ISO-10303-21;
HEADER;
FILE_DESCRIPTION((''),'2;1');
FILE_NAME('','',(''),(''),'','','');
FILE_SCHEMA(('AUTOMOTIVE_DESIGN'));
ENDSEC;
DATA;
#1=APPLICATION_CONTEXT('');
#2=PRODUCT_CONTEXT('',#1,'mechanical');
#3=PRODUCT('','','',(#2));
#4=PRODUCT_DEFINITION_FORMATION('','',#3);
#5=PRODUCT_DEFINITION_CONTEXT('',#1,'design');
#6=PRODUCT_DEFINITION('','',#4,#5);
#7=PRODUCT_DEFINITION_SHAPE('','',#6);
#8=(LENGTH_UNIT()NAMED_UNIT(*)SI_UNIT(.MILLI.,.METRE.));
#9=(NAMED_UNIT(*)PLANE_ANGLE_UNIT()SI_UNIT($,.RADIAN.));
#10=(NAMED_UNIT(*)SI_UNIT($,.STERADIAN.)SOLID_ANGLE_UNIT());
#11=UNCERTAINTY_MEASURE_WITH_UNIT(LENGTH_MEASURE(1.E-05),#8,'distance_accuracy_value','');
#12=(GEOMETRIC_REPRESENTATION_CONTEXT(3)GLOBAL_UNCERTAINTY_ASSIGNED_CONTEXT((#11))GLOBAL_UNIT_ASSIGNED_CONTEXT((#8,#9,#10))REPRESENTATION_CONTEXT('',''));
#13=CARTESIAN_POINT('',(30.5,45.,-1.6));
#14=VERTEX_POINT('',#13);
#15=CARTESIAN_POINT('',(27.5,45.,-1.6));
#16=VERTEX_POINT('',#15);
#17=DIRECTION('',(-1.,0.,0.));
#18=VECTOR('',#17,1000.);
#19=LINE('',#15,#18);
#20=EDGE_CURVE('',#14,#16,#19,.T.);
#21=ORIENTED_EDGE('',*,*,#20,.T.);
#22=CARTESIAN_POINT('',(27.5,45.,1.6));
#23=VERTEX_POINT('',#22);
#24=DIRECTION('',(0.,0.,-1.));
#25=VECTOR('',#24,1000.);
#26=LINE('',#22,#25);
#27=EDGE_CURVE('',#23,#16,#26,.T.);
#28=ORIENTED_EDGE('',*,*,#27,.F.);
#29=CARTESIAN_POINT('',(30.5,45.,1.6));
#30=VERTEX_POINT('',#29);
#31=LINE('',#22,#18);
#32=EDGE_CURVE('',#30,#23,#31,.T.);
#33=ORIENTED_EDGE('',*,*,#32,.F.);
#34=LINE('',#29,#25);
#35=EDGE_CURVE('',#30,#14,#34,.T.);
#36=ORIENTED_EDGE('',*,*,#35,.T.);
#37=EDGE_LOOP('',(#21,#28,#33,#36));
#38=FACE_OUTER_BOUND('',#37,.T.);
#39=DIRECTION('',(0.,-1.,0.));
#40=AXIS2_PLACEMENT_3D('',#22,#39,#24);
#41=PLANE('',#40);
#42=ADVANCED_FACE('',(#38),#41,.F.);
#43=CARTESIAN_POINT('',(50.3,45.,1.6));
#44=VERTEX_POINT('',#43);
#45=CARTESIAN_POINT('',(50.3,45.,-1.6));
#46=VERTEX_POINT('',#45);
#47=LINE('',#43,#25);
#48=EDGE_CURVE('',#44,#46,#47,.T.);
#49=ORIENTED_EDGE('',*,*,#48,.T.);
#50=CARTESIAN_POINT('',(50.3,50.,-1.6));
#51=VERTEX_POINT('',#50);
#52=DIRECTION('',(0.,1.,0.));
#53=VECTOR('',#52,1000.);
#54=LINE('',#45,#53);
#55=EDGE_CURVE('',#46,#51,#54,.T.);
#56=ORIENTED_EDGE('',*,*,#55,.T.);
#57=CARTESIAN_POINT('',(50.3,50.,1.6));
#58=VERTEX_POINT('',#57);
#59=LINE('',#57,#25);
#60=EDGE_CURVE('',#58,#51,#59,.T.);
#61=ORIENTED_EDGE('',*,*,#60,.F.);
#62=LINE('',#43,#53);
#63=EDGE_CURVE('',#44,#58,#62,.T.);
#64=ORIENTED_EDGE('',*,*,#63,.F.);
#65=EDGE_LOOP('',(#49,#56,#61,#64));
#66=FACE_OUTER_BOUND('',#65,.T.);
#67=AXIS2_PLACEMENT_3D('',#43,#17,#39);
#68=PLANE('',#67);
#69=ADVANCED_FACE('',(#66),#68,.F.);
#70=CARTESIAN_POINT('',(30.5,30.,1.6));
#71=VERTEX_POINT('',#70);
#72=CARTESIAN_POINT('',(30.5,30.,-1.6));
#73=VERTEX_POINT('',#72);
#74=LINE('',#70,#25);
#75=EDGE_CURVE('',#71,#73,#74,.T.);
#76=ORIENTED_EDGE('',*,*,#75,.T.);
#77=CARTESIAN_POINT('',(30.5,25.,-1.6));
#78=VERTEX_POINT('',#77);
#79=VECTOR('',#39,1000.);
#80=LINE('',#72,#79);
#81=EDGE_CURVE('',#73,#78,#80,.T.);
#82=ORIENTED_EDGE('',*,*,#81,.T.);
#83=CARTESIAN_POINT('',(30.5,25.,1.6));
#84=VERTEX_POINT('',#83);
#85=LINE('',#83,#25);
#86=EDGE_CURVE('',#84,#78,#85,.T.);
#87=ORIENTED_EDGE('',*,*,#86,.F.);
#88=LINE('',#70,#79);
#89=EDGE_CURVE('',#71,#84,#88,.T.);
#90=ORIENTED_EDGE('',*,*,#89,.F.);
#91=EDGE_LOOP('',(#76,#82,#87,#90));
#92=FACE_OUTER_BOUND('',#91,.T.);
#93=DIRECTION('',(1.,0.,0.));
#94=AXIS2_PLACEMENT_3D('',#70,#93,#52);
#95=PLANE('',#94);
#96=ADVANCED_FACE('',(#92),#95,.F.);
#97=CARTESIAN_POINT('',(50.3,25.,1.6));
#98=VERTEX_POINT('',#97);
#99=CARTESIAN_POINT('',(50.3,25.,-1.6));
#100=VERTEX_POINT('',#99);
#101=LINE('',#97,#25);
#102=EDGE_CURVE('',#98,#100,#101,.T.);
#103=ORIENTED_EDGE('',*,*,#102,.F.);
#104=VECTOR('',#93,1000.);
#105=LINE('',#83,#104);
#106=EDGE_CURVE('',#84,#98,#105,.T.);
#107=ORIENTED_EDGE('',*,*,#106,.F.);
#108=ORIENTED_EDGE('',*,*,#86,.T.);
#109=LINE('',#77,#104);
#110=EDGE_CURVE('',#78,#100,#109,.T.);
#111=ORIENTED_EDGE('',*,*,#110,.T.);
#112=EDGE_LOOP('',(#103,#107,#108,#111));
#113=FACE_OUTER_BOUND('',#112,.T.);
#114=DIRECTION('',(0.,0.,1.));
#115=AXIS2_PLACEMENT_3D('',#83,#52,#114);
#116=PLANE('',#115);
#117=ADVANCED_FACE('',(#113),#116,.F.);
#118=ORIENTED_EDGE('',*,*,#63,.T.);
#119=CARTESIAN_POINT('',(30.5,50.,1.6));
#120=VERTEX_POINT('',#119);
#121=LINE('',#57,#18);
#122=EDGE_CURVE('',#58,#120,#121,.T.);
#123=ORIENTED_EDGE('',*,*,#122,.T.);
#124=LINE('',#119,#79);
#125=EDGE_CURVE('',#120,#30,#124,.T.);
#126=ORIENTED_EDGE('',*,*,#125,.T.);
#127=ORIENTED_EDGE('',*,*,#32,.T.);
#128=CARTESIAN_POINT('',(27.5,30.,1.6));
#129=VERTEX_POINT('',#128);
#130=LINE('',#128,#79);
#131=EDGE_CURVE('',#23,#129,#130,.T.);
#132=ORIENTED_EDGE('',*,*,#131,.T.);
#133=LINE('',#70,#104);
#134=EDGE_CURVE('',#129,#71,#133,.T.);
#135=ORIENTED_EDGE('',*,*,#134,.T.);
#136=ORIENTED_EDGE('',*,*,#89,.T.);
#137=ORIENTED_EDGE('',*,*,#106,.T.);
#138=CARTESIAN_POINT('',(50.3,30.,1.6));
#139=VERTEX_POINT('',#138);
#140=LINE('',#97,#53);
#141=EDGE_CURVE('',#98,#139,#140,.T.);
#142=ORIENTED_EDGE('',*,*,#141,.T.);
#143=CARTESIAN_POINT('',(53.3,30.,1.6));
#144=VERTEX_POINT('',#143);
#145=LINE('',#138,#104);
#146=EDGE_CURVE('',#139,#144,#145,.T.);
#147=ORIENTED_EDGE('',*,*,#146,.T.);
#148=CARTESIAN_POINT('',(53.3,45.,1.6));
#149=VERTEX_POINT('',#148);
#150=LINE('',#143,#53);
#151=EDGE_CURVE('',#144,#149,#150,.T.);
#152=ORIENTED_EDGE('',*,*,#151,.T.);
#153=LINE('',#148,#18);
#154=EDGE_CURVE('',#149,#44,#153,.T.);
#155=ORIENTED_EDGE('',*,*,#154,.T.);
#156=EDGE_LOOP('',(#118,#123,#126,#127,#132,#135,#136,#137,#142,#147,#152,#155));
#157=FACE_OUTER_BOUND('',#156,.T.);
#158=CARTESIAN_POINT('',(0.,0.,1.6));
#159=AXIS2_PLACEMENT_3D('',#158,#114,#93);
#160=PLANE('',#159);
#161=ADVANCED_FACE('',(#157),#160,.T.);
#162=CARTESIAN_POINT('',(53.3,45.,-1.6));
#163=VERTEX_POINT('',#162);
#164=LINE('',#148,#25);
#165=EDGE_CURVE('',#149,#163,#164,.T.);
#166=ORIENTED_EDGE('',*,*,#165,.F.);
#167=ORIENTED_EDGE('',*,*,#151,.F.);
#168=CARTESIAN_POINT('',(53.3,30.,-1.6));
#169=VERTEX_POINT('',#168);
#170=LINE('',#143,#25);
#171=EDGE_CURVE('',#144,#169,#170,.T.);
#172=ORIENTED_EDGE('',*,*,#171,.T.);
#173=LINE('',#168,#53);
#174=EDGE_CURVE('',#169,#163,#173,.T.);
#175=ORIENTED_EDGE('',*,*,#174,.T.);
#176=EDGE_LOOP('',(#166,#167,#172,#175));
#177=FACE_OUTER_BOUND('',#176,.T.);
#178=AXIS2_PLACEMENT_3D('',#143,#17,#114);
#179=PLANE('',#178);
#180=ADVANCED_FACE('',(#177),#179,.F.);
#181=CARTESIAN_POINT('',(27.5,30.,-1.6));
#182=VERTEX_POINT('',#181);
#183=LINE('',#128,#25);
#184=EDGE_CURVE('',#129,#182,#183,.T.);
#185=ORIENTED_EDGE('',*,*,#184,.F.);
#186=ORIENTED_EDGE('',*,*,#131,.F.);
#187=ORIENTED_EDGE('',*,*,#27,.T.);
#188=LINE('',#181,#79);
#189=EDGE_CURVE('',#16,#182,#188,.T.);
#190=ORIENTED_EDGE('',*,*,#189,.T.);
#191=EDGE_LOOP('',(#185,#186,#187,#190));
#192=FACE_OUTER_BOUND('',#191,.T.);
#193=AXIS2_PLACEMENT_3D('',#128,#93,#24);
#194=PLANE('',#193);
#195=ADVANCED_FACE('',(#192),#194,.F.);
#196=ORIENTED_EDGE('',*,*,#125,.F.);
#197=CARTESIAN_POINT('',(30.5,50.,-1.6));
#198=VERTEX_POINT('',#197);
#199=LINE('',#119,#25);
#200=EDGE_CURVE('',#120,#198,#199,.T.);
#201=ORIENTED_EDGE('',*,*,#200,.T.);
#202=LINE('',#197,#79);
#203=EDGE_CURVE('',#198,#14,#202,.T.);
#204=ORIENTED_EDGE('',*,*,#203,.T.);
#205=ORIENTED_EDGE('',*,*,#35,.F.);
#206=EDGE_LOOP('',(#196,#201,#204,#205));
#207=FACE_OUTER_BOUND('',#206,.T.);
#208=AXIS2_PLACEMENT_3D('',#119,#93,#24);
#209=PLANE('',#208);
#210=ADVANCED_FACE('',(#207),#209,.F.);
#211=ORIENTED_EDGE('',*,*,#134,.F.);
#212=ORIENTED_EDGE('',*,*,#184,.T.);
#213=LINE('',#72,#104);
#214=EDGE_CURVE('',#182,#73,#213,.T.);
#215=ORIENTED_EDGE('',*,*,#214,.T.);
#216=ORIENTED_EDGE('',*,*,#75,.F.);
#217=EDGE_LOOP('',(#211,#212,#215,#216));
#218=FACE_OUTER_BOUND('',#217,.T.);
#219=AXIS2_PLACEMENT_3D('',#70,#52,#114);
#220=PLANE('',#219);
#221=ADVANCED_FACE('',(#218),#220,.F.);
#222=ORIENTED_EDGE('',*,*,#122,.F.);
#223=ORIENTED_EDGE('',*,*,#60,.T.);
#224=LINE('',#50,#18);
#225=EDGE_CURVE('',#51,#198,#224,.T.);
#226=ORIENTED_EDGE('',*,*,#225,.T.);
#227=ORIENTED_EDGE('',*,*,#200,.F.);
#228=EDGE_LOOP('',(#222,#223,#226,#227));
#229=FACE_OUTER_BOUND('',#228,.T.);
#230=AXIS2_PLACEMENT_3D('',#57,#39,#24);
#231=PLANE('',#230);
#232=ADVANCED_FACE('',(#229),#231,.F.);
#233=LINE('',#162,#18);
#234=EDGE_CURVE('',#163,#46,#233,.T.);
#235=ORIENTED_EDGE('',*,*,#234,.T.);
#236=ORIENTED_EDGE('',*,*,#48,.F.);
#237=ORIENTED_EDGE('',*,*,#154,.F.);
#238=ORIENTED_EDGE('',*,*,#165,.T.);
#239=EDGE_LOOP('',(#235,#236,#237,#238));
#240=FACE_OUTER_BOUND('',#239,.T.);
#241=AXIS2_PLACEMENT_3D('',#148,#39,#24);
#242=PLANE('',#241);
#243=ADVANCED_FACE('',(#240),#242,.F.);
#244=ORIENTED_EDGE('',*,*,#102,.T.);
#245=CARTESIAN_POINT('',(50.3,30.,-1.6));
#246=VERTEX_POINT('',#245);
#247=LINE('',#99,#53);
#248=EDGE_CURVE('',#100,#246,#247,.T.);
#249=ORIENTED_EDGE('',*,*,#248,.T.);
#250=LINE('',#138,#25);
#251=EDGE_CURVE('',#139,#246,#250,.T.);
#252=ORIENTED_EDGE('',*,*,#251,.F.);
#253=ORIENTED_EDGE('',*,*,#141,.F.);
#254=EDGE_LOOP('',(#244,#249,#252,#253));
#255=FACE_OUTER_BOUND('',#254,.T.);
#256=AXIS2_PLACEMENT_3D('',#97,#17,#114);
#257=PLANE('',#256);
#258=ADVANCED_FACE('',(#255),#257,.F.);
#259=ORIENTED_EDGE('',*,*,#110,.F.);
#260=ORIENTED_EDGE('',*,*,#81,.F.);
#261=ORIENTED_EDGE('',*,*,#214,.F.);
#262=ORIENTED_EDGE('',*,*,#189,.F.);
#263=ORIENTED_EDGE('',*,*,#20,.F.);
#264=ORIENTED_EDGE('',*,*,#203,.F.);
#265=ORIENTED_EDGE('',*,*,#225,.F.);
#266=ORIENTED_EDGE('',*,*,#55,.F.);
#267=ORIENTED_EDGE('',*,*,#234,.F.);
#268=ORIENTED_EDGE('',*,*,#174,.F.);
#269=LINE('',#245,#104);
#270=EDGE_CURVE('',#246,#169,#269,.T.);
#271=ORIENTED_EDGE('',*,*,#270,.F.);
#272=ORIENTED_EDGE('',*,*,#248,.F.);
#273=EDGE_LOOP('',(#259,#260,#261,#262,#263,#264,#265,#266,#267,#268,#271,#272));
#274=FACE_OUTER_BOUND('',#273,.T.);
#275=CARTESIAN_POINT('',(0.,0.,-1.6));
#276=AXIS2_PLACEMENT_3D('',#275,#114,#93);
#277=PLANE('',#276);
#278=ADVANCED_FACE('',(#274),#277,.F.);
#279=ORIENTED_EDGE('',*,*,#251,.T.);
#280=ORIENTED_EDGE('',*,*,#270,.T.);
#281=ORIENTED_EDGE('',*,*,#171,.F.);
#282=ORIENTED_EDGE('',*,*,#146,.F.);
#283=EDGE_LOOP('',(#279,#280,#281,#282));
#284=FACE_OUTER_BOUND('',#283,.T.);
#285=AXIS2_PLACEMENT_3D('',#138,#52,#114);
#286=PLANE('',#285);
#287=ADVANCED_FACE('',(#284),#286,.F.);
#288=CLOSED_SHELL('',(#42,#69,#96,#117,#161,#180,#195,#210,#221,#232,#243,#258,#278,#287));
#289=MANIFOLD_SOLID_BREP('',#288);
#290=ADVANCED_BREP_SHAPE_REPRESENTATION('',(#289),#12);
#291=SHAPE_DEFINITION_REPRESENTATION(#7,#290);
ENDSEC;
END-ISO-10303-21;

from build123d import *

# Parameters (mm, degrees)
BOSS_EXTRUDE1_DEPTH = 1.6


with BuildPart() as part:
    # Sketch1 → Boss-Extrude1 (new, symmetric)
    with BuildSketch(Plane.XY):
        Polygon((30.5, 25), (50.3, 25), (50.3, 30), (53.3, 30), (53.3, 45), (50.3, 45), (50.3, 50), (30.5, 50), (30.5, 45), (27.5, 45), (27.5, 30), (30.5, 30), align=None)
    extrude(amount=BOSS_EXTRUDE1_DEPTH, both=True)


solid = part.part
